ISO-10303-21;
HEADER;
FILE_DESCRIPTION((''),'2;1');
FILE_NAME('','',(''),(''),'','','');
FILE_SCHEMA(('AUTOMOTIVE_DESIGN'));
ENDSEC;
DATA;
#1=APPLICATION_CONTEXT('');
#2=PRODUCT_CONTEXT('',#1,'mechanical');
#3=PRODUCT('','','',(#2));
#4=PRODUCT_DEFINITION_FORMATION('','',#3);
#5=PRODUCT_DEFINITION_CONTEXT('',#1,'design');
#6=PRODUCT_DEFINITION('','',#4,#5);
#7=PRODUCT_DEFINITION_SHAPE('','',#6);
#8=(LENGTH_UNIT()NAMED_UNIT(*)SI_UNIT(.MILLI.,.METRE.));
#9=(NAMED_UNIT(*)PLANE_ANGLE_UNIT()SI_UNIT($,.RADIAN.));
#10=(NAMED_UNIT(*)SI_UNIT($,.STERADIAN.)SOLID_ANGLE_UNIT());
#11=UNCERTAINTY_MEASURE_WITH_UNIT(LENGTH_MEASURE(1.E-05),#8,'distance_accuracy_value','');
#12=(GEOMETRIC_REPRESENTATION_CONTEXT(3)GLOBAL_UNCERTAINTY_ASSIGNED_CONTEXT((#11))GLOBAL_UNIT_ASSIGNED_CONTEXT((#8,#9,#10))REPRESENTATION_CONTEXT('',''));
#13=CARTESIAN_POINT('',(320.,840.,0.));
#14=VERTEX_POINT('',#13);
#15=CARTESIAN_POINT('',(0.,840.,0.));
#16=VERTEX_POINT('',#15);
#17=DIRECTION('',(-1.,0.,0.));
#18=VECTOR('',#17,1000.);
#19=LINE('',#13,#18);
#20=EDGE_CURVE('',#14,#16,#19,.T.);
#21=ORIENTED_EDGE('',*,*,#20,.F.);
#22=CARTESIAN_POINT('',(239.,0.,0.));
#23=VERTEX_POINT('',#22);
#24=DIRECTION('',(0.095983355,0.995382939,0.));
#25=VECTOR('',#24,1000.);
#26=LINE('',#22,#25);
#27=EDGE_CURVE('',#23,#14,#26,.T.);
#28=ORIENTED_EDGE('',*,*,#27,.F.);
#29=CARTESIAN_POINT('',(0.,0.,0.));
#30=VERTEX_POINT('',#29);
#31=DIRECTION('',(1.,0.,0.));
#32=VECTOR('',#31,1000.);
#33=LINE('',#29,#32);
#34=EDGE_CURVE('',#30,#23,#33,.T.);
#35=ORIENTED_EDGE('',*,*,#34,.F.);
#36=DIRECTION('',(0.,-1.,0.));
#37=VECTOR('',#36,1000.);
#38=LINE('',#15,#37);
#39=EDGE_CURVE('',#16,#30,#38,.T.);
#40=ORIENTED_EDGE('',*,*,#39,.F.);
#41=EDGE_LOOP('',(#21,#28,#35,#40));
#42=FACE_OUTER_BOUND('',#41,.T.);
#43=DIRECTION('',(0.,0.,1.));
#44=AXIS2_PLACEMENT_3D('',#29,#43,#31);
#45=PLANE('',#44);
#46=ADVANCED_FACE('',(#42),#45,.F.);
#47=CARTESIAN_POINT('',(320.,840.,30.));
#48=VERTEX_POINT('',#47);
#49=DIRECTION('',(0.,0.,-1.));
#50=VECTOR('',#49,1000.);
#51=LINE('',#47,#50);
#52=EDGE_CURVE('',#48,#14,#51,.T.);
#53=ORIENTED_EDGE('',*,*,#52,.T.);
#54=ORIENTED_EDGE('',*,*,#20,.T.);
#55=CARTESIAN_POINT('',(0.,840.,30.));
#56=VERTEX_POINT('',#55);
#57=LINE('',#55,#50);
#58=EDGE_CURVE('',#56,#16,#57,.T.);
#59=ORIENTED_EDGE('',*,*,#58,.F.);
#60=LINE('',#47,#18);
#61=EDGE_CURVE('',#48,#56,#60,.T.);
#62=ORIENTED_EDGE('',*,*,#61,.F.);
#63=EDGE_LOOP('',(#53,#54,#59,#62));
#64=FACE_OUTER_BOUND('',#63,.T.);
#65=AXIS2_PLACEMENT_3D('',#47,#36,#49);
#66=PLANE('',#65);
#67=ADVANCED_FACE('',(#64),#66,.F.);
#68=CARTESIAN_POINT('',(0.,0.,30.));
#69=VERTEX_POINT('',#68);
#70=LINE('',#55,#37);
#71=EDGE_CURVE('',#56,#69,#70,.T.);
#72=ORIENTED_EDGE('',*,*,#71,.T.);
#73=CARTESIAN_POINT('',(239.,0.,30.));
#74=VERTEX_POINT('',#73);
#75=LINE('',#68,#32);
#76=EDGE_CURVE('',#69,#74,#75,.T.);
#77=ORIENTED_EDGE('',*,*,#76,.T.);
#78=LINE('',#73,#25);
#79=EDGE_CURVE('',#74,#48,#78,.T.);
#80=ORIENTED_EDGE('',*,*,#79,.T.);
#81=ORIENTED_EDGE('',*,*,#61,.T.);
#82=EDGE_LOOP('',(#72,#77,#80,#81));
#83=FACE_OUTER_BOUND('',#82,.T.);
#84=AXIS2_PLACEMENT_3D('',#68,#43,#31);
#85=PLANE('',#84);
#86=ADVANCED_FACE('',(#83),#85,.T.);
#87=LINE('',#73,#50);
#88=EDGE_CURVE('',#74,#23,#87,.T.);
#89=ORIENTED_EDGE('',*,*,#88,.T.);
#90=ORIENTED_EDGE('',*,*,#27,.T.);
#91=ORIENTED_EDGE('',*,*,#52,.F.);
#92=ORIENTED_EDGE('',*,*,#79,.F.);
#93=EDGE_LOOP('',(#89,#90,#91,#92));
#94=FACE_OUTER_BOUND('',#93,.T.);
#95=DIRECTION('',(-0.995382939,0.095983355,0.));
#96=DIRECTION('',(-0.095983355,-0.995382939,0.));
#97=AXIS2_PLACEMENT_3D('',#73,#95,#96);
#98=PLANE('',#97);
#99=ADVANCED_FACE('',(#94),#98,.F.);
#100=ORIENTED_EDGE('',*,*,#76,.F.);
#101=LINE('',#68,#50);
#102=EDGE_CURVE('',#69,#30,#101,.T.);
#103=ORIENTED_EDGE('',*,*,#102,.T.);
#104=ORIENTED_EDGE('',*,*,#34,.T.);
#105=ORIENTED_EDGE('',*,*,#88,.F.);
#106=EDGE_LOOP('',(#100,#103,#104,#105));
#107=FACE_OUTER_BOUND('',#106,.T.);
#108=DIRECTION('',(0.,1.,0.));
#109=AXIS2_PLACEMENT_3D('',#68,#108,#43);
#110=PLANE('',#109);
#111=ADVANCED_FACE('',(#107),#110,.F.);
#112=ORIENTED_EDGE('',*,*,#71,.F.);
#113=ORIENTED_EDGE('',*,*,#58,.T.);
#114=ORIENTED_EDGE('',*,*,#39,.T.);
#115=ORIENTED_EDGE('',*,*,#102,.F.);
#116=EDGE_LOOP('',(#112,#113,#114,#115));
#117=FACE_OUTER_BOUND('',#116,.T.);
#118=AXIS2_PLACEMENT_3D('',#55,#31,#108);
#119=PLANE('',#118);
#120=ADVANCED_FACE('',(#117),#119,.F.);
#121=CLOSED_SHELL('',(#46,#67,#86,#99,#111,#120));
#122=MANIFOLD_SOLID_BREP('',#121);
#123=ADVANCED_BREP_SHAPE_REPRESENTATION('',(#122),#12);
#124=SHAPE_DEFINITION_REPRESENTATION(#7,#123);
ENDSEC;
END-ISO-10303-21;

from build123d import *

# Parameters (mm, degrees)
BOSS_EXTRUDE1_DEPTH = 30


with BuildPart() as part:
    # Sketch1 → Boss-Extrude1 (new body)
    with BuildSketch(Plane.XY):
        Polygon((0, 0), (239, 0), (320, 840), (0, 840), align=None)
    extrude(amount=BOSS_EXTRUDE1_DEPTH)


solid = part.part
